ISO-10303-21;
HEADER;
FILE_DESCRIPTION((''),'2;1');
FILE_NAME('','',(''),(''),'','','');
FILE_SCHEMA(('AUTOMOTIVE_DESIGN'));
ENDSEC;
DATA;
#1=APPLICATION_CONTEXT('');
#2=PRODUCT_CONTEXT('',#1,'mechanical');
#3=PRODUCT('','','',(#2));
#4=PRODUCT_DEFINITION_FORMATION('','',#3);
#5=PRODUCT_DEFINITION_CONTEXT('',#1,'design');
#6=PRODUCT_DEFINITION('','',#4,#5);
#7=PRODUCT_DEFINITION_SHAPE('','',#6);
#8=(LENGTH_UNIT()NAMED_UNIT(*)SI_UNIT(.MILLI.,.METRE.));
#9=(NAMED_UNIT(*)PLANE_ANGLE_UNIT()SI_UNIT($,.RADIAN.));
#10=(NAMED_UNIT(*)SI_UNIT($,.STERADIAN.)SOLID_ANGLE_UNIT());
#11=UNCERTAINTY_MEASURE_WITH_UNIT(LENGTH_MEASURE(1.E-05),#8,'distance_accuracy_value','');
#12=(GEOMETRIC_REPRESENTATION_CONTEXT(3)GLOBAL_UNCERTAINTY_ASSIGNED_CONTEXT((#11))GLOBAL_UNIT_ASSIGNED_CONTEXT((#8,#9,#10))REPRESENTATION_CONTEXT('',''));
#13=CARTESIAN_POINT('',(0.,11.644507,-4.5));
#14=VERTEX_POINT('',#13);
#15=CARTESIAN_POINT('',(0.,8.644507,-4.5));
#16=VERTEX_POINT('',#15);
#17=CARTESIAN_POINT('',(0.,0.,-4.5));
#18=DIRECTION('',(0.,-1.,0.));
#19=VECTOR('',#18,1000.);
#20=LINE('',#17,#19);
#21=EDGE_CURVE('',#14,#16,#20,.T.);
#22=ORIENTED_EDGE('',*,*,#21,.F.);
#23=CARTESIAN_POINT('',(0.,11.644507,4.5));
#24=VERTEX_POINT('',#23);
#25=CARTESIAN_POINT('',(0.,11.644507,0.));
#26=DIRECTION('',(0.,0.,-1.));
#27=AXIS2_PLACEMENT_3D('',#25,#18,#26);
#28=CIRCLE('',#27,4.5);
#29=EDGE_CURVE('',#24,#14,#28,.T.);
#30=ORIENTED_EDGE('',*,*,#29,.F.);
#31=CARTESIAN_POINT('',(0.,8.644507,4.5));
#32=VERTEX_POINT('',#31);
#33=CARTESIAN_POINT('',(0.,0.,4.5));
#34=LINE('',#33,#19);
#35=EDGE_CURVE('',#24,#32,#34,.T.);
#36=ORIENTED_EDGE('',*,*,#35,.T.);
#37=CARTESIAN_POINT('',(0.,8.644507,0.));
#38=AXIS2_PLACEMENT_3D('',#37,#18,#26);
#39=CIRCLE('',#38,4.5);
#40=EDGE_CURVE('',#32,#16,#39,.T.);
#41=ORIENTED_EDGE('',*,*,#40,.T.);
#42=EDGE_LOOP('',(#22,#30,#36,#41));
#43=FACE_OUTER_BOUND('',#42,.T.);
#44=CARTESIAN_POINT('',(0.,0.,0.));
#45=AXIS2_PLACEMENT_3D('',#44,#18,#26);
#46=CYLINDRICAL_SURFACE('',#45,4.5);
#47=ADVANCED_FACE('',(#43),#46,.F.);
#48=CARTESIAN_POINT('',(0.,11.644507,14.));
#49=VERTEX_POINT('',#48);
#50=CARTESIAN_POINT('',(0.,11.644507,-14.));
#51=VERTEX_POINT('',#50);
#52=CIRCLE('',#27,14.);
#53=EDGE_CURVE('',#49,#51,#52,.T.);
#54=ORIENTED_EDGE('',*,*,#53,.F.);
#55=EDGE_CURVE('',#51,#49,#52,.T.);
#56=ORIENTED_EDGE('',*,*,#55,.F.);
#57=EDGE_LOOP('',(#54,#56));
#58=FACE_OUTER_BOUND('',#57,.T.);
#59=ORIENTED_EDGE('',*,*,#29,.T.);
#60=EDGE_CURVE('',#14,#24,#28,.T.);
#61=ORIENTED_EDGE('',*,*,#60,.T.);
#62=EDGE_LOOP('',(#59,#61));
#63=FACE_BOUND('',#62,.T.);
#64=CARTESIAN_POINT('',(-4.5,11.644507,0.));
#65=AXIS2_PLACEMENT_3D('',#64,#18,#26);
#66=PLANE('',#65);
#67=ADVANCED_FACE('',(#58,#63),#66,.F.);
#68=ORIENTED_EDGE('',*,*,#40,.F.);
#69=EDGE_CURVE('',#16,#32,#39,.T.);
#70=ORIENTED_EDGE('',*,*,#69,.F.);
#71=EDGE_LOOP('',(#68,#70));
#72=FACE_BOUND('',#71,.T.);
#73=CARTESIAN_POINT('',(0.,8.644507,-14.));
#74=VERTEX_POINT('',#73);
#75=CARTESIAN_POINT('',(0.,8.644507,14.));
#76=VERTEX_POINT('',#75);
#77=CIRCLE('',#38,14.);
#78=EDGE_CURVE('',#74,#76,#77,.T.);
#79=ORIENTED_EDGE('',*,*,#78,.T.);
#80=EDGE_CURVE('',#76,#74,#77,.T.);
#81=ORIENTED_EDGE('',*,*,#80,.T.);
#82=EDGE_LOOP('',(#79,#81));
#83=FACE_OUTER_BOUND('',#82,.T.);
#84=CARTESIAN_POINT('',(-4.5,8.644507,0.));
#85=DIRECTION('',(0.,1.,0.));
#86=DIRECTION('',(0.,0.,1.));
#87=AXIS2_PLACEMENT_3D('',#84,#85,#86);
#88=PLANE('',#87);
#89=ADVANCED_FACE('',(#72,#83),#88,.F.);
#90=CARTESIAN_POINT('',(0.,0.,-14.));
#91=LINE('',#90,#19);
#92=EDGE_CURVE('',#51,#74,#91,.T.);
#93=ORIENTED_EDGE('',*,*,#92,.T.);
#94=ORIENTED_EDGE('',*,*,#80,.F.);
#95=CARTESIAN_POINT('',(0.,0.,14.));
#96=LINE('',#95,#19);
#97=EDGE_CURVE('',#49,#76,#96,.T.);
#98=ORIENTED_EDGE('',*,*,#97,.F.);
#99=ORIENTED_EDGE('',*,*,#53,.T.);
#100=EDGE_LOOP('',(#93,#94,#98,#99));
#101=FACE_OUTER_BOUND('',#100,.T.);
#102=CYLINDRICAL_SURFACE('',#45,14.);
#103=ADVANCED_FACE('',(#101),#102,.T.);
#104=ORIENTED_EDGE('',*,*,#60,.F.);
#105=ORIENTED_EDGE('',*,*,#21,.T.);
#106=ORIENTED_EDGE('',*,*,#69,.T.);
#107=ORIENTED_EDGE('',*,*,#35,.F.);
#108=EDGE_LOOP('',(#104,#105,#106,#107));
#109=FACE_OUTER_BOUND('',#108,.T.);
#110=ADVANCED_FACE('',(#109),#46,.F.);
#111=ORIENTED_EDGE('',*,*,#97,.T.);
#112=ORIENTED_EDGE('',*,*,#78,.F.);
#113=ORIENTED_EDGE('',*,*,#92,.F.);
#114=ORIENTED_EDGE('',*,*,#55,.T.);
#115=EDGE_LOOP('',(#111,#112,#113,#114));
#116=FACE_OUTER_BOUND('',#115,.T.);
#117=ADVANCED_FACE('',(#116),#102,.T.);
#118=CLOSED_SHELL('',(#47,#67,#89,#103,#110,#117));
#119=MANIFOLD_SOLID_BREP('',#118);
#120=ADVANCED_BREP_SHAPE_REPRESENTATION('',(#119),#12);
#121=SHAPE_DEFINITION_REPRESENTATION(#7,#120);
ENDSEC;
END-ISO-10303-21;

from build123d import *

# Parameters (mm, degrees)
SKETCH_1_W = 9.5
SKETCH_1_H = 3


with BuildPart() as part:
    # 草图1 → Revolve 468 (revolve)
    with BuildSketch(Plane.XY, mode=Mode.PRIVATE) as revolve_468_sk:
        with Locations((-9.25, 10.144507042)):
            Rectangle(SKETCH_1_W, SKETCH_1_H)
    revolve(revolve_468_sk.sketch.rotate(Axis((0, 0, 0), (0, 1, 0)), 270), axis=Axis((0, 0, 0), (0, 1, 0)))


solid = part.part
